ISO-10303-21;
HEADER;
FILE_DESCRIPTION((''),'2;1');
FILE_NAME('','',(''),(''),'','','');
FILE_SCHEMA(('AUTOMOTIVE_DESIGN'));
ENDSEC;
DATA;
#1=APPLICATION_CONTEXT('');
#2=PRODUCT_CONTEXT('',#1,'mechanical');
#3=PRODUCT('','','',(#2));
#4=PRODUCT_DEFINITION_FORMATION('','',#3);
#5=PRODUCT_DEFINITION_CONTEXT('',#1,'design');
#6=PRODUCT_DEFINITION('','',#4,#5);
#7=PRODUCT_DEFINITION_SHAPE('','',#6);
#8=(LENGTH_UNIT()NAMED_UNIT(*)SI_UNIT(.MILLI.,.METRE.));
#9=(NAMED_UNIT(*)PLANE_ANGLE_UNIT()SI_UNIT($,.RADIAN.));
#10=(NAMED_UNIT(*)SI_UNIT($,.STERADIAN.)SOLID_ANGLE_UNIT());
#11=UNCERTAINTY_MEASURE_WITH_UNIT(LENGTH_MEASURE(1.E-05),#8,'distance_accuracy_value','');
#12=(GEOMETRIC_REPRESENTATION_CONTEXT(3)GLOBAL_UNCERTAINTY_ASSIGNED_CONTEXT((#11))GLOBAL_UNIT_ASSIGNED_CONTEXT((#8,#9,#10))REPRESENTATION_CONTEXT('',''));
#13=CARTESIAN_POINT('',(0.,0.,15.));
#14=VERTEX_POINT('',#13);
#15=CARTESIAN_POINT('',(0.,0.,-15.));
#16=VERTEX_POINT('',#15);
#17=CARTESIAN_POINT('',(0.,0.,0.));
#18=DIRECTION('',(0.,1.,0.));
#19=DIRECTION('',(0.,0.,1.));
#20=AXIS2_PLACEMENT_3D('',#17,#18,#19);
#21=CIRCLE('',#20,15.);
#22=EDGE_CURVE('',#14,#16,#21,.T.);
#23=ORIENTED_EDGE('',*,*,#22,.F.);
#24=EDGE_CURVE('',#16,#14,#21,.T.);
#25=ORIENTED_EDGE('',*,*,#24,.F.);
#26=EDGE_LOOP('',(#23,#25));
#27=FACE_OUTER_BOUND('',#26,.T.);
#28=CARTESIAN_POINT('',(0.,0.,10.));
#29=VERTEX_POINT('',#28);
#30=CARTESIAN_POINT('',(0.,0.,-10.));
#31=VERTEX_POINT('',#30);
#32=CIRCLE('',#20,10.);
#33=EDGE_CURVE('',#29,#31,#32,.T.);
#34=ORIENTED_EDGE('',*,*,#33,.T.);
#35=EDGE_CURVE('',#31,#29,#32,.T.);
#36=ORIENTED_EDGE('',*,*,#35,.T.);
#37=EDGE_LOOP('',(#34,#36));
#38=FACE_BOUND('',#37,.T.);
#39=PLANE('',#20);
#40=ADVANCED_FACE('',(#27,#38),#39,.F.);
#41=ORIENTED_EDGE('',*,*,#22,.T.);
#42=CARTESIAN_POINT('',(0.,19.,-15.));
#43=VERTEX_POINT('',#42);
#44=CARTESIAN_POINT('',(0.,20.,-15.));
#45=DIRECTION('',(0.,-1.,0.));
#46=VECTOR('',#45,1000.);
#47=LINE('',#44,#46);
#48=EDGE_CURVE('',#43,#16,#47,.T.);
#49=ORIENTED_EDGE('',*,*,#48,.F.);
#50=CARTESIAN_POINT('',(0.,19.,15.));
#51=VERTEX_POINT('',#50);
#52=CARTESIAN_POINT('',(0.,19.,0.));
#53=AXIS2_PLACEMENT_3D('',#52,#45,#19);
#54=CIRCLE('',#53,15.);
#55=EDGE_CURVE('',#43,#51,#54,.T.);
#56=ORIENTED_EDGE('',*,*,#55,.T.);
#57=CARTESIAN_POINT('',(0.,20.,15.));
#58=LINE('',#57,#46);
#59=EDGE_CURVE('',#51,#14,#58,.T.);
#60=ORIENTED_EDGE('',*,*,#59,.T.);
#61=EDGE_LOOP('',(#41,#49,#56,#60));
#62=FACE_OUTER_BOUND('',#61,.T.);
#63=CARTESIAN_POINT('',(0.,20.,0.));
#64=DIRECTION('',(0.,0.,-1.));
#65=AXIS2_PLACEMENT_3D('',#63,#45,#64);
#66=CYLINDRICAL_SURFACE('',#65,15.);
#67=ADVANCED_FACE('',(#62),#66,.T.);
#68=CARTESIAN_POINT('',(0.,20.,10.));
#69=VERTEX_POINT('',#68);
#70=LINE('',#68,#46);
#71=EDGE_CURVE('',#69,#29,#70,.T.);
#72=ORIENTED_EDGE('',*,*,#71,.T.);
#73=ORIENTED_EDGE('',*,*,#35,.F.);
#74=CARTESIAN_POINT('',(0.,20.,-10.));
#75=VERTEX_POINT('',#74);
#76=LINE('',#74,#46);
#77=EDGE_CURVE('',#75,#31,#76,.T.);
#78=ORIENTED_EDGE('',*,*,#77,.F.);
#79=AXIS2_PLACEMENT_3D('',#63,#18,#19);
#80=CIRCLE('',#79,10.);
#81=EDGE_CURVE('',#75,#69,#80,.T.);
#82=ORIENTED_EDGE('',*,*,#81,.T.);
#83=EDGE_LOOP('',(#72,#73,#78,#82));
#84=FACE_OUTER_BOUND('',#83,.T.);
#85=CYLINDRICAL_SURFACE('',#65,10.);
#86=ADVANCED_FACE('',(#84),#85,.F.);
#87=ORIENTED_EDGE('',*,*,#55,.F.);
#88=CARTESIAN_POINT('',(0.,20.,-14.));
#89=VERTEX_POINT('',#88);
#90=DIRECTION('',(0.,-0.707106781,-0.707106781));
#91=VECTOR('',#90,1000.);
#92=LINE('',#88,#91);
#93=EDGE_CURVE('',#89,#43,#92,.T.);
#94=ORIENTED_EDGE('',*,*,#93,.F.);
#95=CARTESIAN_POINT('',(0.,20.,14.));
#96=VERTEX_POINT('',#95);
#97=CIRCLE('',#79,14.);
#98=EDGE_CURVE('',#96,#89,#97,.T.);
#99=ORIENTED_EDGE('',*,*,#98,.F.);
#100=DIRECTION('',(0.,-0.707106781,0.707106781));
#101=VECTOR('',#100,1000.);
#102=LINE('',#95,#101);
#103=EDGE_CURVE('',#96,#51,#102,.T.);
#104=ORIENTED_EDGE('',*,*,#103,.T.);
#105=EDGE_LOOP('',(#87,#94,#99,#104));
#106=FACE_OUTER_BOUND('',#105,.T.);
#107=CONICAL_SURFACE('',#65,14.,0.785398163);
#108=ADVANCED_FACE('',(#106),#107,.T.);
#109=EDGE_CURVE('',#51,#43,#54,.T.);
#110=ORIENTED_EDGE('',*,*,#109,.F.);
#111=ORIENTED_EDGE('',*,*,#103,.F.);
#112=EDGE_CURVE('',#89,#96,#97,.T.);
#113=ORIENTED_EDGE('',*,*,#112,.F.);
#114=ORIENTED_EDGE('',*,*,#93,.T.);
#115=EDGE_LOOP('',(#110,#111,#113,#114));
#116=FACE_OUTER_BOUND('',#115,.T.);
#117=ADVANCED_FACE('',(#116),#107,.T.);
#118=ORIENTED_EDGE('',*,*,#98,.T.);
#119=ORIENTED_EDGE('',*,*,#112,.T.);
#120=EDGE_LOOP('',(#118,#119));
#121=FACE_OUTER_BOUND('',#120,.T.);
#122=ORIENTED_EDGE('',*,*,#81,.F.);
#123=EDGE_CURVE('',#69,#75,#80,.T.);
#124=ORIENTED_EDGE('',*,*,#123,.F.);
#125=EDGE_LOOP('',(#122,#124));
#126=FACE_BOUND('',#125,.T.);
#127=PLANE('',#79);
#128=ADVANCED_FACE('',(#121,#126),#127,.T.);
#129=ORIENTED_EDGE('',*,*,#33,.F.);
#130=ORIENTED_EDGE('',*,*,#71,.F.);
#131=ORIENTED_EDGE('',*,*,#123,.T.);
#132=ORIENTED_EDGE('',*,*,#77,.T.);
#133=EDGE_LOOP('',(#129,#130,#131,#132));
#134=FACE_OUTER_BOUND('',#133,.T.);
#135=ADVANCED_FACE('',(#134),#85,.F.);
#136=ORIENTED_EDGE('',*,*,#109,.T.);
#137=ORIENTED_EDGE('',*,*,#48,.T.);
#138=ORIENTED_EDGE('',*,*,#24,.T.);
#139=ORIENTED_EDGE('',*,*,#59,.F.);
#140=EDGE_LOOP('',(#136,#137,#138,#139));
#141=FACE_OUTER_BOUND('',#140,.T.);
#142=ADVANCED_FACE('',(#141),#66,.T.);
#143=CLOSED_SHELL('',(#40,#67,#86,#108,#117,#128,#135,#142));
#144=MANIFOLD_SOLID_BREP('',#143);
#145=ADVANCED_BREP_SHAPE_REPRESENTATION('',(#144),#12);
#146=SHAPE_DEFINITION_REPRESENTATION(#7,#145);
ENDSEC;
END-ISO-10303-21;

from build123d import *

# Parameters (mm, degrees)
BUSH_PROFILE_30_20_R         = 15
BUSH_PROFILE_30_20_R_2       = 10
BUSH_BODY_L20_DEPTH          = 20
OUTER_EDGE_CHAMFER_1X45_SIZE = 1


with BuildPart() as part:
    # Bush Profile Ø30-Ø20 → Bush Body L20 (new body)
    with BuildSketch(Plane(origin=(0, 0, 0), x_dir=(1, 0, 0), z_dir=(0, 1, 0))):
        with Locations(Location((0, 0, 0), (0, 0, 270))):
            Circle(BUSH_PROFILE_30_20_R)
        with Locations(Location((0, 0, 0), (0, 0, 270))):
            Circle(BUSH_PROFILE_30_20_R_2, mode=Mode.SUBTRACT)
    extrude(amount=BUSH_BODY_L20_DEPTH)

    # Outer Edge Chamfer 1x45°
    outer_edge_chamfer_1x45_edges = [part.edges().sort_by_distance(p)[0] for p in [
        (0, 20, -15),
    ]]
    chamfer(outer_edge_chamfer_1x45_edges, length=OUTER_EDGE_CHAMFER_1X45_SIZE)


solid = part.part
